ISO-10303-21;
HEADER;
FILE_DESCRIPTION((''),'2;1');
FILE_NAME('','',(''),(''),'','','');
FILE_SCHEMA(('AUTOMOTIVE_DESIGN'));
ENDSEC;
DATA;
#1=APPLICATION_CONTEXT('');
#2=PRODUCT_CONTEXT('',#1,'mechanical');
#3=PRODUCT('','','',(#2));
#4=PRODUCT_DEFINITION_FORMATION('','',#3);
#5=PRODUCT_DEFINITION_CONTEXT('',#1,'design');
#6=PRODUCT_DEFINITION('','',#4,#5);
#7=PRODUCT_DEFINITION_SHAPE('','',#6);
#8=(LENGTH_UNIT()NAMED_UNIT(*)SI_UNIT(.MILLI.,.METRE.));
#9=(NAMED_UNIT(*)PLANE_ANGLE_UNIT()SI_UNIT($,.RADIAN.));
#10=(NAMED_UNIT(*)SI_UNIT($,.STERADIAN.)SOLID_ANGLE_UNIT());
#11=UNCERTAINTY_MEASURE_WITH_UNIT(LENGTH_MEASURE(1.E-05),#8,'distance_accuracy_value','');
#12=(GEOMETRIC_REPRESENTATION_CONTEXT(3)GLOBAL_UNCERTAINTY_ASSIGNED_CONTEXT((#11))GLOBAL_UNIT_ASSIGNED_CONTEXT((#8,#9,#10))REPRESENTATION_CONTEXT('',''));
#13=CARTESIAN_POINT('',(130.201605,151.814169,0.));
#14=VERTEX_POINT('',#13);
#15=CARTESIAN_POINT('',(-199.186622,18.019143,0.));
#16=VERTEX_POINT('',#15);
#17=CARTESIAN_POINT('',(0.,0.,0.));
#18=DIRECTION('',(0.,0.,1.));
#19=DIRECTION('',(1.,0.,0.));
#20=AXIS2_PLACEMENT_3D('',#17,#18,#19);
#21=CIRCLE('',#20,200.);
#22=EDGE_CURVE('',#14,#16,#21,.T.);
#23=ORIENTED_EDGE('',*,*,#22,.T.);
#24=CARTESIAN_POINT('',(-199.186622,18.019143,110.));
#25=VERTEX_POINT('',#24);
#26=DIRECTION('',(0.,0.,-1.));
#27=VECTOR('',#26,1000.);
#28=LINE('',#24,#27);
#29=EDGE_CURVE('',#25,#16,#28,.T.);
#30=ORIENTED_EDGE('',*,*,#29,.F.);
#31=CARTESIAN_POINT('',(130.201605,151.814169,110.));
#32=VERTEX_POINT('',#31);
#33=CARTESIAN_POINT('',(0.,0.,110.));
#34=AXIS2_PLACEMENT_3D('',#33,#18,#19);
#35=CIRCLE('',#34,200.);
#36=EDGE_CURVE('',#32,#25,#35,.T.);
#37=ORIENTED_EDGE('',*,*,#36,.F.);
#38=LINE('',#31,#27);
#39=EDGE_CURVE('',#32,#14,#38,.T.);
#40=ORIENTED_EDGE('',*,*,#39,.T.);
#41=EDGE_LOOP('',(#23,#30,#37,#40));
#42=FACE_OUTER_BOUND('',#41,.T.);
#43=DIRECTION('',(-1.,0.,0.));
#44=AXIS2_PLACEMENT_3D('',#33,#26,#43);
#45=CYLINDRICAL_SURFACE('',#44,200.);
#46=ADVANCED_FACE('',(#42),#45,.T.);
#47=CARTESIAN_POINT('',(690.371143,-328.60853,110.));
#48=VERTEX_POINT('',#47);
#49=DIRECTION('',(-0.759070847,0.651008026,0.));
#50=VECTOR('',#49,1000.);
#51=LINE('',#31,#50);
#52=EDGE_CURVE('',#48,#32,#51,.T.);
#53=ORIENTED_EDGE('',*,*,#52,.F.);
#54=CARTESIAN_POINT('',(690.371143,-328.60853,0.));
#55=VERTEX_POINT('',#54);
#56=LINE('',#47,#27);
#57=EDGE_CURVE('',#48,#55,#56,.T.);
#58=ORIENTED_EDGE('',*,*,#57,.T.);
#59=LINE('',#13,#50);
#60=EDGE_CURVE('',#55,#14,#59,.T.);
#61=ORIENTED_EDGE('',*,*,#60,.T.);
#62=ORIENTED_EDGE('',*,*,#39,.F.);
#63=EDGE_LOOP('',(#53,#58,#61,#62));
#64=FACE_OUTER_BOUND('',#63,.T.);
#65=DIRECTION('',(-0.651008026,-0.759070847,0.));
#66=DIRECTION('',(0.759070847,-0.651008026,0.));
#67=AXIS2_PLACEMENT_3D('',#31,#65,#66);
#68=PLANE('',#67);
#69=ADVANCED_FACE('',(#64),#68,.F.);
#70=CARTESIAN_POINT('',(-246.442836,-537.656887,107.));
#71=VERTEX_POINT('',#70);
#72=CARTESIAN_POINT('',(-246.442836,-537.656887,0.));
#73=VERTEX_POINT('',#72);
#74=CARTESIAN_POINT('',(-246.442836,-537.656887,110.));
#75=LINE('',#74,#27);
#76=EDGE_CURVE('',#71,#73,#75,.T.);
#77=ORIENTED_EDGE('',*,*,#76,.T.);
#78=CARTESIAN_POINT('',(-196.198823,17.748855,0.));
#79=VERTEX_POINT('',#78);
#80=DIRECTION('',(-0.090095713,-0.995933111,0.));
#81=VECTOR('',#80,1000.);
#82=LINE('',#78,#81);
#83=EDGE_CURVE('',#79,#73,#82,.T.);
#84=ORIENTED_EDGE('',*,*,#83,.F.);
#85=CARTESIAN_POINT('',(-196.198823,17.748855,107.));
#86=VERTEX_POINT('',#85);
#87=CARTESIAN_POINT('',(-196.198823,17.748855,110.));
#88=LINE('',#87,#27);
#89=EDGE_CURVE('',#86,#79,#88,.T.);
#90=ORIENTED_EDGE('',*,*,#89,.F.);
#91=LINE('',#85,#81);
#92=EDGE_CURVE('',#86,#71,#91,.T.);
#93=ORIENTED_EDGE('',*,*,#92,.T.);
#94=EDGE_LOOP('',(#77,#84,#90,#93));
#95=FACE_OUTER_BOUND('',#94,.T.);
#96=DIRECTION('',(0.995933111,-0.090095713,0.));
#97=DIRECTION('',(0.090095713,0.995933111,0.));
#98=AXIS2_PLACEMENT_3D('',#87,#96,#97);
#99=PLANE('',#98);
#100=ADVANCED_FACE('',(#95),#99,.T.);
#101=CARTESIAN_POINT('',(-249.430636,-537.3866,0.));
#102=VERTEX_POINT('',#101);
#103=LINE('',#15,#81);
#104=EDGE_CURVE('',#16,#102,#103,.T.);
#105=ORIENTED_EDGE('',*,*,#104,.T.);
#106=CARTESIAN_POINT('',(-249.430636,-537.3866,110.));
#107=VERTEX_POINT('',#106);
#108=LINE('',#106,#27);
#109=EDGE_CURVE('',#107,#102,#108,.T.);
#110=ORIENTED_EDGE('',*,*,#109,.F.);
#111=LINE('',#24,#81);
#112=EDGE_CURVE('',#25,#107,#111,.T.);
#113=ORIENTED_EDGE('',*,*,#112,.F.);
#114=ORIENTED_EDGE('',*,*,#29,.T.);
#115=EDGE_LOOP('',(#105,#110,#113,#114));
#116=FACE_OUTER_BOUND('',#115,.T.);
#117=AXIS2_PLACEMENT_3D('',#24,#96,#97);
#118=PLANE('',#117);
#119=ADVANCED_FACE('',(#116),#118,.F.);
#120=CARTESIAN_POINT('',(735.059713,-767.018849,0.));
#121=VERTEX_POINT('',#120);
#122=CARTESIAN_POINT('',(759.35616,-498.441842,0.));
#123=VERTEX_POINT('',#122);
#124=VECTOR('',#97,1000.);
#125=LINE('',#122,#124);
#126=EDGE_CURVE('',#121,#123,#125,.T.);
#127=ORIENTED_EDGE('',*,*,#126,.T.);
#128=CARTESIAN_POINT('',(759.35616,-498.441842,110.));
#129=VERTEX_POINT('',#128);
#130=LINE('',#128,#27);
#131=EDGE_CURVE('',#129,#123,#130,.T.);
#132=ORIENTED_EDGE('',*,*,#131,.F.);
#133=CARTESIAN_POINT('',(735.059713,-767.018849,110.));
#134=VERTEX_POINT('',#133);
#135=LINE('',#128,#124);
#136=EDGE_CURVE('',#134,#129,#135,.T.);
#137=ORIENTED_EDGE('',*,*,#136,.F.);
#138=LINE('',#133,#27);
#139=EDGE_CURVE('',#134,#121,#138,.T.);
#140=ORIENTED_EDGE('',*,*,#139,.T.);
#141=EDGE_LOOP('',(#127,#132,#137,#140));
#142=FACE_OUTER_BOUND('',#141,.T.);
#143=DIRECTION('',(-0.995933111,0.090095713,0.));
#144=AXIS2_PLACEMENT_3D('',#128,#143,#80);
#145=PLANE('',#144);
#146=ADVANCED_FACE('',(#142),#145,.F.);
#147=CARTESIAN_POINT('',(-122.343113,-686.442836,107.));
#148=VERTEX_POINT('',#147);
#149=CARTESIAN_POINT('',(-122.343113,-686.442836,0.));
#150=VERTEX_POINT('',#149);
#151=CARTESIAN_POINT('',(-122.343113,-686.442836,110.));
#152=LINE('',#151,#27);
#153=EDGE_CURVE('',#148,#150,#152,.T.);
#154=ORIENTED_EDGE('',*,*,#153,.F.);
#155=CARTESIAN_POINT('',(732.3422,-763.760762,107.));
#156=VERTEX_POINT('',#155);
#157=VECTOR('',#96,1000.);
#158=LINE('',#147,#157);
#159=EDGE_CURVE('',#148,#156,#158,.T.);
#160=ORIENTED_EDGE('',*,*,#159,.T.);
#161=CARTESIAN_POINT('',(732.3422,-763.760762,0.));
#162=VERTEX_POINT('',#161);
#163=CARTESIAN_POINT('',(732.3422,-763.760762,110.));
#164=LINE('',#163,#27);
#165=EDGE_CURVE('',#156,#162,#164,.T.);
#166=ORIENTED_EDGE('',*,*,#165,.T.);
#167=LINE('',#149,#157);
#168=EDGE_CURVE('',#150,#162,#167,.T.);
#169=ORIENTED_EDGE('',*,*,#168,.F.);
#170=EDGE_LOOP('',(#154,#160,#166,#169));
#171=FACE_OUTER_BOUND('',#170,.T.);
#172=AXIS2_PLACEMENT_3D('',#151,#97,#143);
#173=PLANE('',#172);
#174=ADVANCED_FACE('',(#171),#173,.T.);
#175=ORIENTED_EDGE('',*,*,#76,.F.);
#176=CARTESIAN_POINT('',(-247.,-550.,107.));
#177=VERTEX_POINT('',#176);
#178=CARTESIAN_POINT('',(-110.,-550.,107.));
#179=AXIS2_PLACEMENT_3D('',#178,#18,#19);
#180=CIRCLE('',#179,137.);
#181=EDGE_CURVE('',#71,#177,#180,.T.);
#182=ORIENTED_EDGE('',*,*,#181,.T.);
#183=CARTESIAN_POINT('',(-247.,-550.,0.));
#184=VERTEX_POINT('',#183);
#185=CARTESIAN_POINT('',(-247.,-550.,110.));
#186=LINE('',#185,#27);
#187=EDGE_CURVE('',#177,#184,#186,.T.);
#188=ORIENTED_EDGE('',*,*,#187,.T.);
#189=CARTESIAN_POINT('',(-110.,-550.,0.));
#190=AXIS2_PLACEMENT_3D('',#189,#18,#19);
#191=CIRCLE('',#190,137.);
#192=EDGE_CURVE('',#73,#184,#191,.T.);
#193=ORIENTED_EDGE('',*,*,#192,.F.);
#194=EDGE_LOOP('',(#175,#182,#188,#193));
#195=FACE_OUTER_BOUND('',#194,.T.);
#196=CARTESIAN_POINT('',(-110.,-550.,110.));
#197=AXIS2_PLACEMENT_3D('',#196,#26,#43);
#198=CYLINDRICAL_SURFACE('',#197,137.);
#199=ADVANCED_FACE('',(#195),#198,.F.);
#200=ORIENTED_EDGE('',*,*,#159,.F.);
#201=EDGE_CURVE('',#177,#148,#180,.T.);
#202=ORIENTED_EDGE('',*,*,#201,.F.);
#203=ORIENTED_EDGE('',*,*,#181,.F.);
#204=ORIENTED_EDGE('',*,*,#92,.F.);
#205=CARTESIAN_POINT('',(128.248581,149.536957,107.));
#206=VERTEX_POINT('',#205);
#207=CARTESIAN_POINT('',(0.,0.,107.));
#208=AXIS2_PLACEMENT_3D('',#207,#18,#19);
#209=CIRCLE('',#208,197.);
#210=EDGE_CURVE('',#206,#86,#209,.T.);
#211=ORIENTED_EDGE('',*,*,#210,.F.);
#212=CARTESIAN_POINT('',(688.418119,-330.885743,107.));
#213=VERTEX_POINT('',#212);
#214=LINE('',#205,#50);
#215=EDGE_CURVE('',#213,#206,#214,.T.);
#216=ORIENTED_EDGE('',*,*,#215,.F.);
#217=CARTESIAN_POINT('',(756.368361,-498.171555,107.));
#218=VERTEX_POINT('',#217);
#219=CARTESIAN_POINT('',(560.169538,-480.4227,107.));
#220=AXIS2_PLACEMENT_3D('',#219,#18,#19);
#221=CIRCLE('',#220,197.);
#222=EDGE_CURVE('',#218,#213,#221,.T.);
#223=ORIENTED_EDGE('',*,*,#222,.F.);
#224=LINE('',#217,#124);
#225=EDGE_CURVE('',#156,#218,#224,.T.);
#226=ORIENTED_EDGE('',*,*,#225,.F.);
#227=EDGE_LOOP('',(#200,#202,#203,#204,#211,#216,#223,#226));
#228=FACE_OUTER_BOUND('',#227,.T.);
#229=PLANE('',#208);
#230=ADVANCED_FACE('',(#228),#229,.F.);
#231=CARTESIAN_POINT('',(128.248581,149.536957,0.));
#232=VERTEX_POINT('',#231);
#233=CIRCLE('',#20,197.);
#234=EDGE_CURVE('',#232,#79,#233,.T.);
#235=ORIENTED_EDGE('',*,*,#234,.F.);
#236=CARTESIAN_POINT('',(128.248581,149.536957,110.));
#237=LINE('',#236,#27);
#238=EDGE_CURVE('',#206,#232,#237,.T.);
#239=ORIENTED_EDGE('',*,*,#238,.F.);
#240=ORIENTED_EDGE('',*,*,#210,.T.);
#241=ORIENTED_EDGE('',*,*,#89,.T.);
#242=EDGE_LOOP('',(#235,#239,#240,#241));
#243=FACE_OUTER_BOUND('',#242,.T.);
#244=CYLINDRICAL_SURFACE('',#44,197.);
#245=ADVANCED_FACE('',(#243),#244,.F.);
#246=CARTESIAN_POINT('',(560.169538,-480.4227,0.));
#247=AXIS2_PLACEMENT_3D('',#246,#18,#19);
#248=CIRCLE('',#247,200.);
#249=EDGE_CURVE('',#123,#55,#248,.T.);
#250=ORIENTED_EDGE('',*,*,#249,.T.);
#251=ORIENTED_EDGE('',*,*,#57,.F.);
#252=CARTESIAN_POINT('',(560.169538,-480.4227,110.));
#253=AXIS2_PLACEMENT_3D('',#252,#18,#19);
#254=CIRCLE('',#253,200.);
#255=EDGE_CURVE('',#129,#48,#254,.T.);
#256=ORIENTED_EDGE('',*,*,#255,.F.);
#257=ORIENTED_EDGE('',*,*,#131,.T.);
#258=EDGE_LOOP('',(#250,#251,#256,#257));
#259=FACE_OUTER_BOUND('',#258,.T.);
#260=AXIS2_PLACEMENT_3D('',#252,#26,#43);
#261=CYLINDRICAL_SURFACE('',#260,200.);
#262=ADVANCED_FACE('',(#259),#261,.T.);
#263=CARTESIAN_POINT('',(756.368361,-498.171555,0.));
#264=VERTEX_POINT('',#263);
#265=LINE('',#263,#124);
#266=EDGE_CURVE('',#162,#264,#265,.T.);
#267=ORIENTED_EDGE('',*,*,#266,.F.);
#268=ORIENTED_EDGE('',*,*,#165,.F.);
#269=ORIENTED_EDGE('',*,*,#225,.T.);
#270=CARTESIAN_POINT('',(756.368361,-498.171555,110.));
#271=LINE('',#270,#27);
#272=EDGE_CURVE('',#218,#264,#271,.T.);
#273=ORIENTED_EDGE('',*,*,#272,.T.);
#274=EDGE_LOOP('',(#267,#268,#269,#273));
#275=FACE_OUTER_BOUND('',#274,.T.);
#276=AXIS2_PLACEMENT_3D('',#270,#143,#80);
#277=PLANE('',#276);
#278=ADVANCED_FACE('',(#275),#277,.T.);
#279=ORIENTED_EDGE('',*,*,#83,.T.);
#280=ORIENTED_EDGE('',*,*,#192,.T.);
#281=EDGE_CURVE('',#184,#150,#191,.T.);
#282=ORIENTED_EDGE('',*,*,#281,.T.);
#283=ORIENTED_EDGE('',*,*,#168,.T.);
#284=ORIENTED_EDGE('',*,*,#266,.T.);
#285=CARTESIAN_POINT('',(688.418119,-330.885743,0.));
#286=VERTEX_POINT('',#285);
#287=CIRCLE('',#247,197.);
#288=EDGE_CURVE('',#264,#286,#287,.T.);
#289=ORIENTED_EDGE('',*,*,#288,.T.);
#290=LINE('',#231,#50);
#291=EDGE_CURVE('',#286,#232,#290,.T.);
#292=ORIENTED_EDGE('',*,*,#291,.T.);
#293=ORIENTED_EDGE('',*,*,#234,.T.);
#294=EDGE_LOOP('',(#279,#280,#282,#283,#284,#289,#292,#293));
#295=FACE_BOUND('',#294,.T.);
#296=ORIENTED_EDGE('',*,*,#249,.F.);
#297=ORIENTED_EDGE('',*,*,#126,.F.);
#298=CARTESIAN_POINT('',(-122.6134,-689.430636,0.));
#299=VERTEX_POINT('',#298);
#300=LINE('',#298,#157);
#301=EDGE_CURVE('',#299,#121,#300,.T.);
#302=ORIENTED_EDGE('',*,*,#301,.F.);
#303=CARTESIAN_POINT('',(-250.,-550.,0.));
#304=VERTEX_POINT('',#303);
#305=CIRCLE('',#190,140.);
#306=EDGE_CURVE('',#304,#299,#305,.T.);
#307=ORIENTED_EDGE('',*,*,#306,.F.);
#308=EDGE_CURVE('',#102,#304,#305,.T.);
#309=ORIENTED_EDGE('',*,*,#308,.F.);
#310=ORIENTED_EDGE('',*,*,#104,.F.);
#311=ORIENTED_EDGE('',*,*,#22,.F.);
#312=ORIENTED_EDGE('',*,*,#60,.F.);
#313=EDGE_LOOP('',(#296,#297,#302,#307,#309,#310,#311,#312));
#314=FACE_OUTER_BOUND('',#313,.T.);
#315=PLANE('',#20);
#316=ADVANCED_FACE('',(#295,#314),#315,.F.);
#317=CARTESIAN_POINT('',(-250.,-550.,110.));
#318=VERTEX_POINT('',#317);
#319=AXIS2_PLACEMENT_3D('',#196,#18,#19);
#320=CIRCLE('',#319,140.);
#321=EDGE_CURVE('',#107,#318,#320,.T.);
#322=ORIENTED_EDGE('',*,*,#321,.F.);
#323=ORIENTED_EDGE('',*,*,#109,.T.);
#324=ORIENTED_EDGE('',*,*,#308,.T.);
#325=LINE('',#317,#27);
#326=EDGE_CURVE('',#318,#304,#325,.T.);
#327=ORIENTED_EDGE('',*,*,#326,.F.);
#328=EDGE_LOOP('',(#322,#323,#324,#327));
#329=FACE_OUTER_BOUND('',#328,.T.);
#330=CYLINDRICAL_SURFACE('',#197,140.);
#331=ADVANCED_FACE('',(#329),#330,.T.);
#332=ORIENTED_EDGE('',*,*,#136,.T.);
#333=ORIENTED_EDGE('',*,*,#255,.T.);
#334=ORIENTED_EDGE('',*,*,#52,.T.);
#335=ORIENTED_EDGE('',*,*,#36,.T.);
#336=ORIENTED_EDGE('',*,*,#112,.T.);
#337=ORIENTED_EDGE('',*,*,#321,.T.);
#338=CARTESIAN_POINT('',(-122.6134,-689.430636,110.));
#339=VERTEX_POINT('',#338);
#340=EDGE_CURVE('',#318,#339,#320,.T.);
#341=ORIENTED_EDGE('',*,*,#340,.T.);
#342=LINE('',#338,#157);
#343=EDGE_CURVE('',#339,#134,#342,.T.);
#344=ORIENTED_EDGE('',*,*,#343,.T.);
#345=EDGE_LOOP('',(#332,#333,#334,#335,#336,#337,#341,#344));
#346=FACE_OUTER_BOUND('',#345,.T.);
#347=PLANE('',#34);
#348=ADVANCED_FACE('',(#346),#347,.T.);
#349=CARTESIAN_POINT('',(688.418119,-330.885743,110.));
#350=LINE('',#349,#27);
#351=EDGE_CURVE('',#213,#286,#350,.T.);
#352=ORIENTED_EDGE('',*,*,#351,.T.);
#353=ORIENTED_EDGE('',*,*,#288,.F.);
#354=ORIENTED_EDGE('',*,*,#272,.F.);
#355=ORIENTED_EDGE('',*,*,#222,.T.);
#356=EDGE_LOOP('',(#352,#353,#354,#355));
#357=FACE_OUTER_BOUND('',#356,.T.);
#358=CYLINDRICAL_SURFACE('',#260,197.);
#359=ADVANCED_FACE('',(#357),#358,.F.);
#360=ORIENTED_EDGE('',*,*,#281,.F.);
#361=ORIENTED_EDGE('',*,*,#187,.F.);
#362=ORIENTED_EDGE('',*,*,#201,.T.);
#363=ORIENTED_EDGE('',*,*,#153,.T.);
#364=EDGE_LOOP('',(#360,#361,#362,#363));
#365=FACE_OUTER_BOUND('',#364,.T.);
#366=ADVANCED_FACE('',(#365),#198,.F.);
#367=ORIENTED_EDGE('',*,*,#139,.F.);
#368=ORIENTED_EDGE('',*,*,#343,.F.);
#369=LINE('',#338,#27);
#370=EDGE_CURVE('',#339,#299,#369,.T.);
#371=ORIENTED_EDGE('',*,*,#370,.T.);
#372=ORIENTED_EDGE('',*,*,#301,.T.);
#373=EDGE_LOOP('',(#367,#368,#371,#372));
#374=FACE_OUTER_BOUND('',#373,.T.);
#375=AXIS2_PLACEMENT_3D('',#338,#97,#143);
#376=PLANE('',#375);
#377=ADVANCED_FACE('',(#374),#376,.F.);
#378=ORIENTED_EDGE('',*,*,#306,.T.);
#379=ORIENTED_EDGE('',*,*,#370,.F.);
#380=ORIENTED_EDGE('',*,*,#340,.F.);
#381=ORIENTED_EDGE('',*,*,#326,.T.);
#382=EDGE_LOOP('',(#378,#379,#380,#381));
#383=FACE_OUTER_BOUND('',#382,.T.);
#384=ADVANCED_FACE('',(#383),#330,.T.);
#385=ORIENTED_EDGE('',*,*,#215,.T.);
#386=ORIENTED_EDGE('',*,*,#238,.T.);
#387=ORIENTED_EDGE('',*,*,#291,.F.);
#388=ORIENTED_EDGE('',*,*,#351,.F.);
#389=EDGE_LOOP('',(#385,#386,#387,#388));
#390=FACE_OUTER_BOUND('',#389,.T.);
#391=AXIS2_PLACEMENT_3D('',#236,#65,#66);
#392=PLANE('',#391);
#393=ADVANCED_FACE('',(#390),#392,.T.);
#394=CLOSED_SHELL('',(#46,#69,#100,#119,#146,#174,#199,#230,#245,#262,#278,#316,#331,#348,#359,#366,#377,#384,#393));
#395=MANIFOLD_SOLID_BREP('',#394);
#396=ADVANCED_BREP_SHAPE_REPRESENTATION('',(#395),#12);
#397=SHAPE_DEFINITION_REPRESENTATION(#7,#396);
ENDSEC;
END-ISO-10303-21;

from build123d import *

# Parameters (mm, degrees)
BOSS_EXTRUDE2_DEPTH = 110
SHELL2_T            = -3


with BuildPart() as part:
    # Sketch1 → Boss-Extrude2 (new body)
    with BuildSketch(Plane.XY):
        with BuildLine():
            Line((-199.186622288, 18.019142639), (-249.430635602, -537.386600152))
            ThreePointArc((-249.430635602, -537.386600152), (-217.511368505, -639.673327373), (-122.613399848, -689.430635602))
            Line((-122.613399848, -689.430635602), (735.059712531, -767.018848969))
            Line((735.059712531, -767.018848969), (759.356160444, -498.441842272))
            ThreePointArc((759.356160444, -498.441842272), (745.466568798, -405.15643604), (690.371143367, -328.608530331))
            Line((690.371143367, -328.608530331), (130.201605211, 151.814169301))
            ThreePointArc((130.201605211, 151.814169301), (-75.266263592, 185.297030642), (-199.186622288, 18.019142639))
        make_face()
    extrude(amount=BOSS_EXTRUDE2_DEPTH)

    # Shell2
    shell2_openings = [part.faces().sort_by_distance(p)[0] for p in [
        (206.21225605, -348.127169203, 0),
    ]]
    offset(amount=SHELL2_T, openings=shell2_openings, kind=Kind.INTERSECTION)


solid = part.part
